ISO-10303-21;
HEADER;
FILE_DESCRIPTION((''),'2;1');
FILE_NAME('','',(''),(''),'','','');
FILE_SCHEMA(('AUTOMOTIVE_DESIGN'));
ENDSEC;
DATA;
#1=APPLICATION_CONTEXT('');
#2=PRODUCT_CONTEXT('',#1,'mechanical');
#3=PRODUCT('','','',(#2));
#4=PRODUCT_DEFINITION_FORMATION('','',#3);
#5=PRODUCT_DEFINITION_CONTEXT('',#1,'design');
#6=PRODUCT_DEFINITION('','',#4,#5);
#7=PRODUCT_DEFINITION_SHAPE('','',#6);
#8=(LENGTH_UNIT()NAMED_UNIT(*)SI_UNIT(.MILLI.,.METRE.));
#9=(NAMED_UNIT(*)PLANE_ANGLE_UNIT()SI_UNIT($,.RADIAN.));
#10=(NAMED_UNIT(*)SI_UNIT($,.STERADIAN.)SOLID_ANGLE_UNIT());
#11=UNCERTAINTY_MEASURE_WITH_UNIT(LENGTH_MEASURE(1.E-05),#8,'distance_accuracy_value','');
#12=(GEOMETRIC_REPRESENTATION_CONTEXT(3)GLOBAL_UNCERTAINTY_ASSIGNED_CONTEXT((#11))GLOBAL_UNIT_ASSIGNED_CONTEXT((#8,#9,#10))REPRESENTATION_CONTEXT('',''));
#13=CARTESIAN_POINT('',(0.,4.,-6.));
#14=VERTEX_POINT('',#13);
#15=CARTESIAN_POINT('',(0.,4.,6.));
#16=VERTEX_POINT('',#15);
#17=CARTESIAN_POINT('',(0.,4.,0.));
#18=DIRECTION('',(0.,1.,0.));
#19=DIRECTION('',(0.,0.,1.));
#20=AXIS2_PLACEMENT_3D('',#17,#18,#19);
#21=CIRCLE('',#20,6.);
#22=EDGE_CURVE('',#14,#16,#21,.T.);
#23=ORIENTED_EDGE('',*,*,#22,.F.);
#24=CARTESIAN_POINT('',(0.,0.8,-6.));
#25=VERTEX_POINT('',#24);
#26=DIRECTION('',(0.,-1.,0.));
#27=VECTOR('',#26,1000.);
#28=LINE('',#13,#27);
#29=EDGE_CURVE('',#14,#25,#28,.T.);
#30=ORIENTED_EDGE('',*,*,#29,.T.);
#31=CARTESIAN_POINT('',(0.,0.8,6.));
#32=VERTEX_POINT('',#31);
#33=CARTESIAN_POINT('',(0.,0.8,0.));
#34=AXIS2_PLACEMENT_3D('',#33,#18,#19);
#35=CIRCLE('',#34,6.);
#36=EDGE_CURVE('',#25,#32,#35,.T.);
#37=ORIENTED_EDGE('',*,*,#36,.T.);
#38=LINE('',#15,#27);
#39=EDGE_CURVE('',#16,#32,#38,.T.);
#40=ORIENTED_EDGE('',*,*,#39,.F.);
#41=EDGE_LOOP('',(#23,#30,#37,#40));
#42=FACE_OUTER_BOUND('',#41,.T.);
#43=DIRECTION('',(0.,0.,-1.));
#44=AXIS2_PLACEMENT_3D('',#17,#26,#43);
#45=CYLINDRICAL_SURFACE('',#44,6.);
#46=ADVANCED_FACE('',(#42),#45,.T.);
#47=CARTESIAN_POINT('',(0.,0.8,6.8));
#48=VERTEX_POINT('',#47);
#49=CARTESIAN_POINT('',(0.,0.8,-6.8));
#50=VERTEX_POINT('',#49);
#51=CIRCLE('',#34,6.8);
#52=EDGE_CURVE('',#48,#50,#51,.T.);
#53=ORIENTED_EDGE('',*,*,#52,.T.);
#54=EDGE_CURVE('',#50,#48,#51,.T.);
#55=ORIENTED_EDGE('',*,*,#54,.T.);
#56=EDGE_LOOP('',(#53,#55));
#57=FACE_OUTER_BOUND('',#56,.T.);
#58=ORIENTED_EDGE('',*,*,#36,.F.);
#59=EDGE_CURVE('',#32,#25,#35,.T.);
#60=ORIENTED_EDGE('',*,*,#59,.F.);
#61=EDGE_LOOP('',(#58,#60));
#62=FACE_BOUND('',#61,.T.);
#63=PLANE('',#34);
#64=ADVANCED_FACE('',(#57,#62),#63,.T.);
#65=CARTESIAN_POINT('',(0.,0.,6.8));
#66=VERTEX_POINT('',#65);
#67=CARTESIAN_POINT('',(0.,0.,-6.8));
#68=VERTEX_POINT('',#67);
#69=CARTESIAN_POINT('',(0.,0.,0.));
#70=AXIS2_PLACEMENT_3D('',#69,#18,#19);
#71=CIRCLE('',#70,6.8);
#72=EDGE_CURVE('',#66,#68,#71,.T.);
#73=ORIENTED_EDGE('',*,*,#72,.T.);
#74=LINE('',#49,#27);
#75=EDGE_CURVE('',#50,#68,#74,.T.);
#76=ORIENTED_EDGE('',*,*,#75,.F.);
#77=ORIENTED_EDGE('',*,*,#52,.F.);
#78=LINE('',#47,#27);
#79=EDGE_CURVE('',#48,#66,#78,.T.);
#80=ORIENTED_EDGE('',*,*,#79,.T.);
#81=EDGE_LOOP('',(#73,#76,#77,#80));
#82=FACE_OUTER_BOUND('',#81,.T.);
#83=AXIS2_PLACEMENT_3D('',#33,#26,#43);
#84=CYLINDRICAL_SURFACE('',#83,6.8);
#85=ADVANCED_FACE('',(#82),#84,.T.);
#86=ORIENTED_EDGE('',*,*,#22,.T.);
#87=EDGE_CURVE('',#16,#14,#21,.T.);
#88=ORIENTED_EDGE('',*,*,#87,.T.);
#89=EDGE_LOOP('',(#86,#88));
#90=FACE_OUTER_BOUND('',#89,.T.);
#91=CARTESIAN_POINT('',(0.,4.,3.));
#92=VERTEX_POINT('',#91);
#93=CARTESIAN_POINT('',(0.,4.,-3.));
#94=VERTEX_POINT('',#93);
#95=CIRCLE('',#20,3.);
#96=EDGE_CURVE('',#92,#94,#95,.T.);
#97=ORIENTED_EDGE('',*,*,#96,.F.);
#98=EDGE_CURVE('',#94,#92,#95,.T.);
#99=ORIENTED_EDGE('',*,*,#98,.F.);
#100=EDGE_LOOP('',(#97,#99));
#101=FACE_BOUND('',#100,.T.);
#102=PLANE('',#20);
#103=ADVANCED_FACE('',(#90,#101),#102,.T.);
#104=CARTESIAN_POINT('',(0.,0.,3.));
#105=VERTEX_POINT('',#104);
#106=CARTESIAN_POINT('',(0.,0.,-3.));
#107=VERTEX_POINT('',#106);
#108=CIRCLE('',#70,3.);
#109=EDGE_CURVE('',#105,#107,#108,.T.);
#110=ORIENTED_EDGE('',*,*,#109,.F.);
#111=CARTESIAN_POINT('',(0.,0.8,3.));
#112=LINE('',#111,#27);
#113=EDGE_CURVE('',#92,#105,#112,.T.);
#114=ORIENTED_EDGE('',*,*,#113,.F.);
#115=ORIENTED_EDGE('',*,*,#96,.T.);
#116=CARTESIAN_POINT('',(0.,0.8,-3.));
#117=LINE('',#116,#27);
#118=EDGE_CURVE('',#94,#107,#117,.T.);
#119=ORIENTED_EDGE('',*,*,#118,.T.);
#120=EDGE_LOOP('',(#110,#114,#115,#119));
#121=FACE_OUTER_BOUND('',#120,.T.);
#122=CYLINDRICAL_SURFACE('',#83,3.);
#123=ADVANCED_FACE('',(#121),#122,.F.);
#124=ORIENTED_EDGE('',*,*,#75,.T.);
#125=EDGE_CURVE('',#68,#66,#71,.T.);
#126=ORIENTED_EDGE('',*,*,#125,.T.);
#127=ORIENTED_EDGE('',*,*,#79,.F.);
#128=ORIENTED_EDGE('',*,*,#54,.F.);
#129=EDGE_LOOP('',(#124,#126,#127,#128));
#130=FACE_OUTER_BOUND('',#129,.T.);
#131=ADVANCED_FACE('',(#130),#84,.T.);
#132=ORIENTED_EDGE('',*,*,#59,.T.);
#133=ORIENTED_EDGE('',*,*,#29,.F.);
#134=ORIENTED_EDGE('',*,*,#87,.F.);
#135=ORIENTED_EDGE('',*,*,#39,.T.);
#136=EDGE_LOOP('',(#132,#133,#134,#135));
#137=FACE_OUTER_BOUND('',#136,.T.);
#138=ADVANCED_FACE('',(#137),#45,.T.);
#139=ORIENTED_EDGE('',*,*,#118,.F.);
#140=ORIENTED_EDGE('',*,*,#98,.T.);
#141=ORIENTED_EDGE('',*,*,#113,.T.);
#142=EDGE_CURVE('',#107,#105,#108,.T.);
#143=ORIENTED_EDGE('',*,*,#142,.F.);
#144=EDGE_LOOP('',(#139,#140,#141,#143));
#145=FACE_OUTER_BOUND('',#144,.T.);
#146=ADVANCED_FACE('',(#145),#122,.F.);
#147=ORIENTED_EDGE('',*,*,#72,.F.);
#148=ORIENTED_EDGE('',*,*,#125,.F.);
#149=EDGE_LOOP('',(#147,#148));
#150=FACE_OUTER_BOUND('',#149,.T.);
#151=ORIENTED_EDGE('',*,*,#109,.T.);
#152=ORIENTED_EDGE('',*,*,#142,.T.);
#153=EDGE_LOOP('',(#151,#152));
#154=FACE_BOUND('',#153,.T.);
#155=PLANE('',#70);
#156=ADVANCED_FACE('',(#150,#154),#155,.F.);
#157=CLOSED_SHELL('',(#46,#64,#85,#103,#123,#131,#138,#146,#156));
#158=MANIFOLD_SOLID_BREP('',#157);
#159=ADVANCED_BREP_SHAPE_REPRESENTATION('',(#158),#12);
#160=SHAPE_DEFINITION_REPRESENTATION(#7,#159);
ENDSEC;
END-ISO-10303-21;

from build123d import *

# Parameters (mm, degrees)
SKETCH_1_R      = 6.8
SKETCH_1_R_2    = 3
EXTRUDE_1_DEPTH = 0.8
SKETCH_2_R      = 6
SKETCH_2_R_2    = 3
EXTRUDE_2_DEPTH = 3.2


with BuildPart() as part:
    # 草图1 → 凸台-拉伸1 (new body)
    with BuildSketch(Plane(origin=(0, 0, 0), x_dir=(1, 0, 0), z_dir=(0, 1, 0))):
        with Locations(Location((0, 0, 0), (0, 0, 270))):
            Circle(SKETCH_1_R)
        with Locations(Location((0, 0, 0), (0, 0, 270))):
            Circle(SKETCH_1_R_2, mode=Mode.SUBTRACT)
    extrude(amount=EXTRUDE_1_DEPTH)

    # 草图2 → 凸台-拉伸2 (add)
    with BuildSketch(Plane(origin=(0, 0.8, 0), x_dir=(1, 0, 0), z_dir=(0, 1, 0))):
        with Locations(Location((0, 0, 0), (0, 0, 270))):
            Circle(SKETCH_2_R)
        with Locations(Location((0, 0, 0), (0, 0, 270))):
            Circle(SKETCH_2_R_2, mode=Mode.SUBTRACT)
    extrude(amount=EXTRUDE_2_DEPTH)


solid = part.part
